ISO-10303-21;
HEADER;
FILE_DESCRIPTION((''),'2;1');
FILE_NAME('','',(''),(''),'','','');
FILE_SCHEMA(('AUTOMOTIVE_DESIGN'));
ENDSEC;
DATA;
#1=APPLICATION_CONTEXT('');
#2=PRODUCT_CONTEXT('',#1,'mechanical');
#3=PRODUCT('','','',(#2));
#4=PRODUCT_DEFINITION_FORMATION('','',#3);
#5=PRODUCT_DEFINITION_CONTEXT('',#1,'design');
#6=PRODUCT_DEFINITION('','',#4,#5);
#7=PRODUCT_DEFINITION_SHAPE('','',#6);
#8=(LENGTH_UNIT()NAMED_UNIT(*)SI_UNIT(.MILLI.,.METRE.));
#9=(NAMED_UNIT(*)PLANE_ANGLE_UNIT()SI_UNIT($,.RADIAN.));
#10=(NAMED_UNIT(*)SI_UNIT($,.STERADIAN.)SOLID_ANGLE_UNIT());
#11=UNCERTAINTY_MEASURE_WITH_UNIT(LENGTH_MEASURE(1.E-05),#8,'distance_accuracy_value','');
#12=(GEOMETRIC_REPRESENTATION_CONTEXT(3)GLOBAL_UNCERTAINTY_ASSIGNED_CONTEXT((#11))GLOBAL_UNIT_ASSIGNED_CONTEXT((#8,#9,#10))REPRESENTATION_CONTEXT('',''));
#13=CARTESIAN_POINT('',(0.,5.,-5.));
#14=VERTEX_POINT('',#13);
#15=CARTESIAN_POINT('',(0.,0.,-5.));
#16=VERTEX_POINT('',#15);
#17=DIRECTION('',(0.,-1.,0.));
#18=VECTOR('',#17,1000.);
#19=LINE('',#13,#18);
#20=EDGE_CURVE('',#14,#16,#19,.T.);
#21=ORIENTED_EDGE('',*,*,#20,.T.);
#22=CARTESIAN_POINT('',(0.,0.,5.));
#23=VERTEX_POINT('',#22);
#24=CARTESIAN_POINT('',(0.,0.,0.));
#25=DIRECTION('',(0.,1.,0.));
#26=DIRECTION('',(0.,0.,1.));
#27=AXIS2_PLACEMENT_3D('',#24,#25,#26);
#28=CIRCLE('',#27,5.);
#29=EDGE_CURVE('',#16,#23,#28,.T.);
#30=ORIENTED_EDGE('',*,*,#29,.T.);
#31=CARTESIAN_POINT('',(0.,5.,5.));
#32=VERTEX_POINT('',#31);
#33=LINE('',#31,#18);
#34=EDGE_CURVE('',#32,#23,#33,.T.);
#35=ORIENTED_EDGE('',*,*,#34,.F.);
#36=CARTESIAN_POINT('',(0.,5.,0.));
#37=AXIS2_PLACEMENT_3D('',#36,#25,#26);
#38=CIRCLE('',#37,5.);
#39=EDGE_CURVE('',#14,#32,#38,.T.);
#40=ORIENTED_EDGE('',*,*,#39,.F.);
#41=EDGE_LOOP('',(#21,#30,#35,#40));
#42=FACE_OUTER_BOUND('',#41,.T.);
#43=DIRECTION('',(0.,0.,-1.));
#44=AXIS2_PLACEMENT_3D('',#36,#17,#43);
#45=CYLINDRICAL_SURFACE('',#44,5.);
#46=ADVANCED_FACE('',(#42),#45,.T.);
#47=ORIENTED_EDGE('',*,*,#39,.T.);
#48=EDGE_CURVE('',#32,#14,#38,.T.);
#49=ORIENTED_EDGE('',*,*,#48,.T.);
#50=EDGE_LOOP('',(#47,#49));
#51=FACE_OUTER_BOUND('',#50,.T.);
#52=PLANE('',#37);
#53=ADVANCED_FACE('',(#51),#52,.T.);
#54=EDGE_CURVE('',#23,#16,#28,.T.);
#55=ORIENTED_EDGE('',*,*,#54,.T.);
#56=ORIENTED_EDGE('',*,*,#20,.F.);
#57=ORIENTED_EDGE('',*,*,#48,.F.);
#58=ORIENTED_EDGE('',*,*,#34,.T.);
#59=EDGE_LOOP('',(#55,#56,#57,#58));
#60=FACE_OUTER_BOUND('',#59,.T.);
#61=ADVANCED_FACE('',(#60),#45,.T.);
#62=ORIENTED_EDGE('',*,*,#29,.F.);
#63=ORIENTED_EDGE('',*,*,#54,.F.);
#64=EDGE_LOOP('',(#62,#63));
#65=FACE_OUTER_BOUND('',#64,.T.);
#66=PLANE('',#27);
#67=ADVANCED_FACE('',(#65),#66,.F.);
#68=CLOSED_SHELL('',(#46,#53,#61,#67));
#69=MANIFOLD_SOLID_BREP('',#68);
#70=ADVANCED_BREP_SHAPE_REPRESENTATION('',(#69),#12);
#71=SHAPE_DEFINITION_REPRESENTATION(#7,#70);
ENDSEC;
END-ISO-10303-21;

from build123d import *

# Parameters (mm, degrees)
SKETCH1_R           = 5
BOSS_EXTRUDE1_DEPTH = 5


with BuildPart() as part:
    # Sketch1 → Boss-Extrude1 (new body)
    with BuildSketch(Plane(origin=(0, 0, 0), x_dir=(1, 0, 0), z_dir=(0, 1, 0))):
        with Locations(Location((0, 0, 0), (0, 0, 270))):
            Circle(SKETCH1_R)
    extrude(amount=BOSS_EXTRUDE1_DEPTH)


solid = part.part
